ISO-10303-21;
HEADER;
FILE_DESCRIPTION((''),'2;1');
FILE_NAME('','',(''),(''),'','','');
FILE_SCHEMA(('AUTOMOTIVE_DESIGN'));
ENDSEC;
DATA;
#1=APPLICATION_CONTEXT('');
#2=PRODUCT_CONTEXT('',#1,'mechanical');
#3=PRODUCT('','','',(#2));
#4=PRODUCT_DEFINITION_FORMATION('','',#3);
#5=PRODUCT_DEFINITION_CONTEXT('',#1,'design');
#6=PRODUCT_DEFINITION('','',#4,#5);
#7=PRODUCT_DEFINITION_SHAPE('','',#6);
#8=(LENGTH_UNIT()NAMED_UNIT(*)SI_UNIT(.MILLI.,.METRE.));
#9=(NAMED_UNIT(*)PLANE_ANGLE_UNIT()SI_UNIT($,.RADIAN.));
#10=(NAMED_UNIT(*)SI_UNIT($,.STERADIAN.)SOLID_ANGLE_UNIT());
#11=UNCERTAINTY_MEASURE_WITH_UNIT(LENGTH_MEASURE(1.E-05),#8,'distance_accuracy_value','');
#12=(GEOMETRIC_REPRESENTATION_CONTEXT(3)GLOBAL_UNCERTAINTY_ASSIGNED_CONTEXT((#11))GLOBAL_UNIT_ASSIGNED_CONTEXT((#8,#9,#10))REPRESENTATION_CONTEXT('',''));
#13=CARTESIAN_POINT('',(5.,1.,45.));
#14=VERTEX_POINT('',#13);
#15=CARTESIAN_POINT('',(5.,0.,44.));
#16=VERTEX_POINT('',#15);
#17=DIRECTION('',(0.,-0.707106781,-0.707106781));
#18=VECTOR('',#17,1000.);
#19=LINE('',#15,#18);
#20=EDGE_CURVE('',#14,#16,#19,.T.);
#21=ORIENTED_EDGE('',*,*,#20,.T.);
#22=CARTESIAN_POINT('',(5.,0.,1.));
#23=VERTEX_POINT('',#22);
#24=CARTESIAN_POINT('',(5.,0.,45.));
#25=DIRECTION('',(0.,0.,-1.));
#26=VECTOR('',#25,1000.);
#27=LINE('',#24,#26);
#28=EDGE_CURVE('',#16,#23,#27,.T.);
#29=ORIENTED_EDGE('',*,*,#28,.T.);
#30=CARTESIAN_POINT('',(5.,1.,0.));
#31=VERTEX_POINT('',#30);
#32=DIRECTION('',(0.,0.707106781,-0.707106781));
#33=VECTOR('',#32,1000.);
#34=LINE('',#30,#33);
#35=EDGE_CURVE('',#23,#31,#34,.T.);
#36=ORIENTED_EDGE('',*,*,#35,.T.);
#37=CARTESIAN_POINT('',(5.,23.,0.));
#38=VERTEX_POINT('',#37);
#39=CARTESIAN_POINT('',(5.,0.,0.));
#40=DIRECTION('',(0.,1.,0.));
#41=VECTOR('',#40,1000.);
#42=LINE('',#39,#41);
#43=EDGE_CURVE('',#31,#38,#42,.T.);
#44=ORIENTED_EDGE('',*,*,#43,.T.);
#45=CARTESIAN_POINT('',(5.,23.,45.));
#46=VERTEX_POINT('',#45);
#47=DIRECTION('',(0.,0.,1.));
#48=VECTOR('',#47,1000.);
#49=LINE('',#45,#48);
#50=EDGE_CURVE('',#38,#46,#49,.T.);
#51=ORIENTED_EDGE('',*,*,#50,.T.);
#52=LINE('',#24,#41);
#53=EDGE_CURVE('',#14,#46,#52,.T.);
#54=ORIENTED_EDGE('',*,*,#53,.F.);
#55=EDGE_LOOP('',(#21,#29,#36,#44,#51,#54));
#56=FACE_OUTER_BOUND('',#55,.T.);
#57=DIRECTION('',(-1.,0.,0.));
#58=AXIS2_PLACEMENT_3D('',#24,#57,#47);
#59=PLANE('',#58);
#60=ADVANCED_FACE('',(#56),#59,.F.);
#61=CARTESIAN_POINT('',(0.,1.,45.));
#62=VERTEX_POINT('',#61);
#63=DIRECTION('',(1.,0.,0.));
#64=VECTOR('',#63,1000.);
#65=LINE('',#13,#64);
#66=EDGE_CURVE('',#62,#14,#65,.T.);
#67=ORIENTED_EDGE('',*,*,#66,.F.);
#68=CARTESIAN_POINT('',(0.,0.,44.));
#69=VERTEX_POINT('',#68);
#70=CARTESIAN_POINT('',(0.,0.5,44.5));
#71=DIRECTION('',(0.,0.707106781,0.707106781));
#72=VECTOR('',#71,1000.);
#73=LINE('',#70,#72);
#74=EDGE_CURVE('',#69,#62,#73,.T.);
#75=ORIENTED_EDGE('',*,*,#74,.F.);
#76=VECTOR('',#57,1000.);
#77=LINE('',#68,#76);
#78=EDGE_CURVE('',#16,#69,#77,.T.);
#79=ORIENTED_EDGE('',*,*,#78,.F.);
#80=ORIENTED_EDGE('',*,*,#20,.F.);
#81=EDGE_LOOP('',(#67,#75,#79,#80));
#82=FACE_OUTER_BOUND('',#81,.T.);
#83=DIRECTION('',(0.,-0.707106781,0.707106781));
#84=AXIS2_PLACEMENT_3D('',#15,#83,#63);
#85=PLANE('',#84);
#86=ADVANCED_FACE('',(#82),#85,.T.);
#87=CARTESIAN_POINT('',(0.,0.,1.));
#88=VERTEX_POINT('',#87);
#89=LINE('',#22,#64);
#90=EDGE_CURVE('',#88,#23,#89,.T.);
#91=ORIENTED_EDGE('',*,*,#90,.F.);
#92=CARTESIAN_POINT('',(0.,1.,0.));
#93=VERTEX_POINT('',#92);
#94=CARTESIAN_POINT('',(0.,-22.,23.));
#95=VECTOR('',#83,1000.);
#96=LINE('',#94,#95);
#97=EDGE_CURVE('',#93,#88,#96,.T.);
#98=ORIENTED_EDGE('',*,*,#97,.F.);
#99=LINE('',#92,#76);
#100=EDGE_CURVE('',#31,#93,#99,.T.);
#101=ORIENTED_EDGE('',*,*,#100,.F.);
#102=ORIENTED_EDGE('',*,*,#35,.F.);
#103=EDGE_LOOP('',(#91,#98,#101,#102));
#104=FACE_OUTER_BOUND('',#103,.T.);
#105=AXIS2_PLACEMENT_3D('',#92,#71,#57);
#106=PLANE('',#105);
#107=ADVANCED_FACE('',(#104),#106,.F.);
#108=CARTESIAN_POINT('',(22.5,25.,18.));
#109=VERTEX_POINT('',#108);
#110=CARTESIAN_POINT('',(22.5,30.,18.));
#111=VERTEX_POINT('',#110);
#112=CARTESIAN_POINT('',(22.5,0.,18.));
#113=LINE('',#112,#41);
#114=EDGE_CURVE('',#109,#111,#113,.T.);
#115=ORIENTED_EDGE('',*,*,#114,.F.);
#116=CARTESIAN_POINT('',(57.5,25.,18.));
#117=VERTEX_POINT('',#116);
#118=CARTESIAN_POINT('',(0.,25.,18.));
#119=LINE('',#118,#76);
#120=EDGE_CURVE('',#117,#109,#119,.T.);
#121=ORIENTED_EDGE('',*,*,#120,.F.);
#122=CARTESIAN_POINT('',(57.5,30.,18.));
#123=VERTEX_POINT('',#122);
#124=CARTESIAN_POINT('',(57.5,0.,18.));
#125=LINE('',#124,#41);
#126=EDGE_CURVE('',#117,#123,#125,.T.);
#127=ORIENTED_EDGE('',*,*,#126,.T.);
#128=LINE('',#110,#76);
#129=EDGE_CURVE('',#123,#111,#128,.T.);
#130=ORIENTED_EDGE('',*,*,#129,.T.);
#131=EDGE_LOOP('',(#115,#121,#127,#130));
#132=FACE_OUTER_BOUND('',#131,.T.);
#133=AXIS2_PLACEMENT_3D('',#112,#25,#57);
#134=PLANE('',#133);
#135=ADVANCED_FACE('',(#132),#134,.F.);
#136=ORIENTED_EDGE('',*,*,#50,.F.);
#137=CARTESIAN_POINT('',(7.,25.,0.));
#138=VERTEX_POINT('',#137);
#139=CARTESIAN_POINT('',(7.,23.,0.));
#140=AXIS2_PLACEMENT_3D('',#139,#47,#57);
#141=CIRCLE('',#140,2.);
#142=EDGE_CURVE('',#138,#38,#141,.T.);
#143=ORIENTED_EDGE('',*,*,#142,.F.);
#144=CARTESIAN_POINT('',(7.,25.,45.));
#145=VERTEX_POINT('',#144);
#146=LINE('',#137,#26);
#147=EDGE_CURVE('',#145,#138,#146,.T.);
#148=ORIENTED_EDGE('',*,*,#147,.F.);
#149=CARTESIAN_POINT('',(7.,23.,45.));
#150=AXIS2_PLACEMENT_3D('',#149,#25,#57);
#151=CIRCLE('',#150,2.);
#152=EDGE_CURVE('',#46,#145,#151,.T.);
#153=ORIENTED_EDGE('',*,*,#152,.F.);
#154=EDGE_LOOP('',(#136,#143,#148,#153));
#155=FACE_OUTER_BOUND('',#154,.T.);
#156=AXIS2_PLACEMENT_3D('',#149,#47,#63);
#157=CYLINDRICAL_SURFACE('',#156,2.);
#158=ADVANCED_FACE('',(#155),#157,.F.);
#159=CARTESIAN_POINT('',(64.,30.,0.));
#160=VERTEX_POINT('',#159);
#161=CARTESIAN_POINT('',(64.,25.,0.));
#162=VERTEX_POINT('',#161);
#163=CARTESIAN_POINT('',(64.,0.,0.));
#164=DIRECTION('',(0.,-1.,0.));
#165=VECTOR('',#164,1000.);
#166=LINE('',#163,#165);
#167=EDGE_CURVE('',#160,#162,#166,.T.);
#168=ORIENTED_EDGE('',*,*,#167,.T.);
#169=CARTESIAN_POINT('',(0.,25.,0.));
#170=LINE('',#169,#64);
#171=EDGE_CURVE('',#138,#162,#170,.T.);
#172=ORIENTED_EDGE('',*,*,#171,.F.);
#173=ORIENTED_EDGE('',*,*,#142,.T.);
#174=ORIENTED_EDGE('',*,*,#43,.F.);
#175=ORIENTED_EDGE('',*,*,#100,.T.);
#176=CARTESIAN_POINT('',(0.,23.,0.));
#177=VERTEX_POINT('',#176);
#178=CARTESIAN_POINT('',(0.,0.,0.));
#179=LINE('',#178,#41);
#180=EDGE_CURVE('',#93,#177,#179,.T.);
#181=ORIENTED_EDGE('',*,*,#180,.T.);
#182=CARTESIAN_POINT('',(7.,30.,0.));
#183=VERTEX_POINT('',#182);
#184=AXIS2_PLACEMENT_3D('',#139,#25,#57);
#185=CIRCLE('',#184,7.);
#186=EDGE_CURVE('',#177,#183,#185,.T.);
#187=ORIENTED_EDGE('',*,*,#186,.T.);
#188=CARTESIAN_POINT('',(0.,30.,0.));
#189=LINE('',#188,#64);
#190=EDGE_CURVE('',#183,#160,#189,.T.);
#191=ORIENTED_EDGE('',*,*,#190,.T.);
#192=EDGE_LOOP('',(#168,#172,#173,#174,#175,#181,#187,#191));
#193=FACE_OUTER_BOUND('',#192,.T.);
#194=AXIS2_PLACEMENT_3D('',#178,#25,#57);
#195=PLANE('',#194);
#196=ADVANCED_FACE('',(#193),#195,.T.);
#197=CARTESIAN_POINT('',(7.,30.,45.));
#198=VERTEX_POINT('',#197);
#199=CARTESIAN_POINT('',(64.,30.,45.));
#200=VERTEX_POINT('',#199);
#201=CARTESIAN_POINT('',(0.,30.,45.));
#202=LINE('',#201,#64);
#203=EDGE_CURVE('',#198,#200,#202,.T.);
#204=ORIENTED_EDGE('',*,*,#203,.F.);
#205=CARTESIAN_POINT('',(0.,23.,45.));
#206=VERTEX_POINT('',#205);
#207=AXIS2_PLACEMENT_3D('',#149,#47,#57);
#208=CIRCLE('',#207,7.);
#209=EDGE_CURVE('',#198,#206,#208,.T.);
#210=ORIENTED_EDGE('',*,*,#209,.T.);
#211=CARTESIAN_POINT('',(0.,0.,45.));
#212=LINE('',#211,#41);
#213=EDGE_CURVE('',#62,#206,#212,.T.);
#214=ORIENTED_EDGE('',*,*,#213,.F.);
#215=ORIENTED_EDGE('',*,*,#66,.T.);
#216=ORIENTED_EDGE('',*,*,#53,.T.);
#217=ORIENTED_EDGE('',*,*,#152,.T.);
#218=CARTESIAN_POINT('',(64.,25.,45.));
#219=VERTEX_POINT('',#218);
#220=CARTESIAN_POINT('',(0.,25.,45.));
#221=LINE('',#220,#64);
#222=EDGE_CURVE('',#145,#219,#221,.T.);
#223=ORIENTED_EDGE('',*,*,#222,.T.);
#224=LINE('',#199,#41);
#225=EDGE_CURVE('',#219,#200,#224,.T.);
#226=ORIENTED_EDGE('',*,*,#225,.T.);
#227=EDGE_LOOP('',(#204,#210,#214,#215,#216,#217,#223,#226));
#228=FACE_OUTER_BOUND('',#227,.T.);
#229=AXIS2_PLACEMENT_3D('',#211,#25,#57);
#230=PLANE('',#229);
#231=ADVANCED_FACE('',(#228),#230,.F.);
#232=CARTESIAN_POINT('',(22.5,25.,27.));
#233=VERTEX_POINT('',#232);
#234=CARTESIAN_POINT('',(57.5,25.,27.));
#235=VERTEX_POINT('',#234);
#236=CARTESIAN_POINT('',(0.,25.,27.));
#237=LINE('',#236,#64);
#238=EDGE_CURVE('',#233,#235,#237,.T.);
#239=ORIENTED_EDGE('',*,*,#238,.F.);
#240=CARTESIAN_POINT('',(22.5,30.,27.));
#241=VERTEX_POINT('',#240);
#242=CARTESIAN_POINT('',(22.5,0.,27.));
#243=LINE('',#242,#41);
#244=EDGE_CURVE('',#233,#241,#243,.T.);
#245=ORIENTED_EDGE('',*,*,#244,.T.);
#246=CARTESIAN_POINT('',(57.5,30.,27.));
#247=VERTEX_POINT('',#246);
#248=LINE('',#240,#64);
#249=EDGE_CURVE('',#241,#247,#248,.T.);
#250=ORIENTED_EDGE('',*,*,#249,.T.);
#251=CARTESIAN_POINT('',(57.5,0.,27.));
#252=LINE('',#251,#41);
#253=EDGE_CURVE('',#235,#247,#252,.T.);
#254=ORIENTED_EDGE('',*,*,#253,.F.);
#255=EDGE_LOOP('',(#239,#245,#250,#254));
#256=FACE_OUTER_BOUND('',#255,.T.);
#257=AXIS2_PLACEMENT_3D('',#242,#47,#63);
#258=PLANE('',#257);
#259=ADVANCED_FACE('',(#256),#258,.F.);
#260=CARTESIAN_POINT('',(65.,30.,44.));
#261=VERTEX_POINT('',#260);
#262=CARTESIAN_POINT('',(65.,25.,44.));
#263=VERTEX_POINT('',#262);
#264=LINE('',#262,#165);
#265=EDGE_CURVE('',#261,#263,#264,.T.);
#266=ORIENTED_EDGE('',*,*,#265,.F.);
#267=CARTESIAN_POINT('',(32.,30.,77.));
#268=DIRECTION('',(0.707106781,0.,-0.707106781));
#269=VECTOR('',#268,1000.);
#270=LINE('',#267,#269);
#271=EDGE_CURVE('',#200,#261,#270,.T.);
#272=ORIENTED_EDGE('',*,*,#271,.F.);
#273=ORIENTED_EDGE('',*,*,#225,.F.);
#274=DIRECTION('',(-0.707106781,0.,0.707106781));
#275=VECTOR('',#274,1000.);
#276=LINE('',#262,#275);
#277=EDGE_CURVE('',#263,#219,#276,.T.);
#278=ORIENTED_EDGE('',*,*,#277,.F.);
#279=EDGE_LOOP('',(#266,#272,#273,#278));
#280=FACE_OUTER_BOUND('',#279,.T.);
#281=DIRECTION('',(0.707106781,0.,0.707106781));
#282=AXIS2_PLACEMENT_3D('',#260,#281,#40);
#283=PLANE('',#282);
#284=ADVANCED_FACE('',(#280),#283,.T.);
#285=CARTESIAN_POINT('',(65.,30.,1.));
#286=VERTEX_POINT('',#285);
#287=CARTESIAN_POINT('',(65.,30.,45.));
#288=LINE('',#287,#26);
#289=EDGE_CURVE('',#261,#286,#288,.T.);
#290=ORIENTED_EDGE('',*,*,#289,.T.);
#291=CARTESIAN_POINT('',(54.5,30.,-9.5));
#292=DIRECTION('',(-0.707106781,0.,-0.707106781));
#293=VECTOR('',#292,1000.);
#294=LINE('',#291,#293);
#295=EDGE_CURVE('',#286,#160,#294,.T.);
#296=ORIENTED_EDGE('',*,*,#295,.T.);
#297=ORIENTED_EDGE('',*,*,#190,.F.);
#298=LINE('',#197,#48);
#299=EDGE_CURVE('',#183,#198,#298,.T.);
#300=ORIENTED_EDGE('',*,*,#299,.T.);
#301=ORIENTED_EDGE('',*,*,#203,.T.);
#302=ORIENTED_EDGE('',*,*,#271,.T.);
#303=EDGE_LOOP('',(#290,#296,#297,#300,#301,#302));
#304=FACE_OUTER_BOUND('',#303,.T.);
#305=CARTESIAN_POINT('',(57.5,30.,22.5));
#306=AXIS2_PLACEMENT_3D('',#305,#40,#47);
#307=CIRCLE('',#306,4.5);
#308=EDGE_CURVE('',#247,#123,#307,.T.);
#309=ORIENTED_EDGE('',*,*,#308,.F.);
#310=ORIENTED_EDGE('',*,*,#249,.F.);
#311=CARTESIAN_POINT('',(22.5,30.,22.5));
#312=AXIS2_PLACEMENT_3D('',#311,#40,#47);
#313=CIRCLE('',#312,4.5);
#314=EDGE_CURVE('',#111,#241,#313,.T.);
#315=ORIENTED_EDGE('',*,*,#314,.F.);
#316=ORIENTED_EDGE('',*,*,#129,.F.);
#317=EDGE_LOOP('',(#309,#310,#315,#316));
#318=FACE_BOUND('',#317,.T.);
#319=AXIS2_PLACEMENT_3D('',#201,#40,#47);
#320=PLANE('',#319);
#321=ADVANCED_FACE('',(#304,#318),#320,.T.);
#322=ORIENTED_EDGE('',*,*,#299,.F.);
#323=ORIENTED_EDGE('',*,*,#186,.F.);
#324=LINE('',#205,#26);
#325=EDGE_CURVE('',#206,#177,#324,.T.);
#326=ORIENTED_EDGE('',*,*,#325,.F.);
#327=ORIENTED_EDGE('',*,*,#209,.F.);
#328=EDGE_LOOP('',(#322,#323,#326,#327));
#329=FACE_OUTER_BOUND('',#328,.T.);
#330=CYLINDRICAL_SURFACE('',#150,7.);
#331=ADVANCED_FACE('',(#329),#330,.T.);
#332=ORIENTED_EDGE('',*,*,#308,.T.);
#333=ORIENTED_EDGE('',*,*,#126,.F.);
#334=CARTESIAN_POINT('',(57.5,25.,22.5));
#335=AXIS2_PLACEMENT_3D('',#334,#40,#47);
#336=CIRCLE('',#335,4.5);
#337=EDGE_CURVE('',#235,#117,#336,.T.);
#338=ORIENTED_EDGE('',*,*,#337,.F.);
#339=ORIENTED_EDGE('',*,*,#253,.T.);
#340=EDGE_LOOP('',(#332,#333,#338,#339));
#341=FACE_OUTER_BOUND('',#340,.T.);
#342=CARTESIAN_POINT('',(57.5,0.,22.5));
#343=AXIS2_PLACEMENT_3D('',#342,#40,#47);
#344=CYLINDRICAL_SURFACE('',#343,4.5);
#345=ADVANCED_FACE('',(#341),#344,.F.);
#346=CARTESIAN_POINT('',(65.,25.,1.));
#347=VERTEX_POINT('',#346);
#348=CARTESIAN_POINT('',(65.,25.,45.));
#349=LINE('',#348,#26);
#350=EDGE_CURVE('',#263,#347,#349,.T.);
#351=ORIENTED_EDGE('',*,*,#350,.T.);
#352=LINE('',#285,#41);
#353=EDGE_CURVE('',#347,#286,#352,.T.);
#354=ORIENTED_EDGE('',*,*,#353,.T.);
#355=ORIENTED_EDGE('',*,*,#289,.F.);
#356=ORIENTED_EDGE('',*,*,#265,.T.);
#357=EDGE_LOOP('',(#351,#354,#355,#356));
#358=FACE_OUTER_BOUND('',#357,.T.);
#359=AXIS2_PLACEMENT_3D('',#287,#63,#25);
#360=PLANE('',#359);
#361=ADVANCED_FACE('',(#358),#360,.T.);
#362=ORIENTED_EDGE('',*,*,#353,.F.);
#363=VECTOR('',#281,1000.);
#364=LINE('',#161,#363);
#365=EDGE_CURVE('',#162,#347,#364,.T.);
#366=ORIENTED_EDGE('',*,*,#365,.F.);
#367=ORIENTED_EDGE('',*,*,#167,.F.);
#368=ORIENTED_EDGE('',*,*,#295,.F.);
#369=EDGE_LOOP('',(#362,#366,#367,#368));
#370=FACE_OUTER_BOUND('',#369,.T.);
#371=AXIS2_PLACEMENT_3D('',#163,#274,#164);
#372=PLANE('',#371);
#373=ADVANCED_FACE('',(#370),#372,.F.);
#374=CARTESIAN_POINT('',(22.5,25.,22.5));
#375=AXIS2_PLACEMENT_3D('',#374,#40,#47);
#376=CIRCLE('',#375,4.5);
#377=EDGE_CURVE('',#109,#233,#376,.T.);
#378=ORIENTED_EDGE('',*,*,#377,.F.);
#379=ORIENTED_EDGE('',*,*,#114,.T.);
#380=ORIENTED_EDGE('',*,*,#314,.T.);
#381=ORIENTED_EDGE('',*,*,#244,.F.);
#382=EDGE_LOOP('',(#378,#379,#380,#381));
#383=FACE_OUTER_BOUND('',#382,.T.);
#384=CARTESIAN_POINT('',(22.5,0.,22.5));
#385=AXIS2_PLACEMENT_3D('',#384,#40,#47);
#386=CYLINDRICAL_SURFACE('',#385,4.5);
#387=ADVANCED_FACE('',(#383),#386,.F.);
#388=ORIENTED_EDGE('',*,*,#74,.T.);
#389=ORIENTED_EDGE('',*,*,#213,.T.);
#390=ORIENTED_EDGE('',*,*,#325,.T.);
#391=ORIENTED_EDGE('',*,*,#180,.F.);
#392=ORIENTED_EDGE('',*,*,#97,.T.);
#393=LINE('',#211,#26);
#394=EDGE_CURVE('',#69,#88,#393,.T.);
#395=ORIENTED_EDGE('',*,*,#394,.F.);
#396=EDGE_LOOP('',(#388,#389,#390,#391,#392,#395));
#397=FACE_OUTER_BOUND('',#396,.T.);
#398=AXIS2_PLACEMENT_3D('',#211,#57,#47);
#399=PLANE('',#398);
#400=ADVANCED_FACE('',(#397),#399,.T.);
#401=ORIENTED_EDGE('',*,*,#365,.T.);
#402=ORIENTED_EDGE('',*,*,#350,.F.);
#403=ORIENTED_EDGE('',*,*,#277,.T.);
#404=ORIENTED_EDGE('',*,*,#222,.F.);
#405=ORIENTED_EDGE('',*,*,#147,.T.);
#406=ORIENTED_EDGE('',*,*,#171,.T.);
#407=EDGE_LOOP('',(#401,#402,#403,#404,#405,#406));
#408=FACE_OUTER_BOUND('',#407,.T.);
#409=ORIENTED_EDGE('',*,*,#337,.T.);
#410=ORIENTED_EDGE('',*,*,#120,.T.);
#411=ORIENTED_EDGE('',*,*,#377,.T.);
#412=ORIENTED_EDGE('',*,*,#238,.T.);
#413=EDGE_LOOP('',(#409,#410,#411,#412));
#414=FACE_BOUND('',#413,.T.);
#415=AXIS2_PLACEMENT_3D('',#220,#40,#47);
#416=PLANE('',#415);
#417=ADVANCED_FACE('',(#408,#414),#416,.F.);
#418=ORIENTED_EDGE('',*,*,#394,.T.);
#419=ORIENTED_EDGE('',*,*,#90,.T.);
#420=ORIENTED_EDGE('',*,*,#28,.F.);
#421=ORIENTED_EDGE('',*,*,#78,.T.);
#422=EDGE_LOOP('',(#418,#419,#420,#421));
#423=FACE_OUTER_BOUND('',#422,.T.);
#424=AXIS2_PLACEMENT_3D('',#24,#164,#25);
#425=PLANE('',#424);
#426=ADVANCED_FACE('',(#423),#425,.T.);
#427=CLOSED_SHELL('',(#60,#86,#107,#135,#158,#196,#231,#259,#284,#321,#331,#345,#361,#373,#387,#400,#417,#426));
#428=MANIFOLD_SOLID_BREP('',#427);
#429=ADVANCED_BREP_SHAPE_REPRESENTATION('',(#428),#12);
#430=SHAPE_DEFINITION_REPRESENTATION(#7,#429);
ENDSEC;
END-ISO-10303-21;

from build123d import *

# Parameters (mm, degrees)
EXTRUDE_1_DEPTH     = 45
FILLET_1_R          = 2
FILLET_2_R          = 7
CHAMFER_1_SIZE      = 1
CUT_EXTRUDE_1_DEPTH = 85.557672626


with BuildPart() as part:
    # 草图1 → 拉伸-薄壁1 (new body)
    with BuildSketch(Plane.XY):
        Polygon((0, 0), (0, 30), (65, 30), (65, 25), (5, 25), (5, 0), align=None)
    extrude(amount=EXTRUDE_1_DEPTH)

    # 圆角1
    fillet_1_edges = [part.edges().sort_by_distance(p)[0] for p in [
        (5, 25, 22.5),
    ]]
    fillet(fillet_1_edges, radius=FILLET_1_R)

    # 圆角2
    fillet_2_edges = [part.edges().sort_by_distance(p)[0] for p in [
        (0, 30, 22.5),
    ]]
    fillet(fillet_2_edges, radius=FILLET_2_R)

    # 倒角1
    chamfer_1_edges = [part.edges().sort_by_distance(p)[0] for p in [
        (2.5, 0, 45),
        (2.5, 0, 0),
        (65, 27.5, 0),
        (65, 27.5, 45),
    ]]
    chamfer(chamfer_1_edges, length=CHAMFER_1_SIZE)

    # 草图2 → 切除-拉伸1 (cut, through all)
    with BuildSketch(Plane(origin=(0, 30, 0), x_dir=(1, 0, 0), z_dir=(0, 1, 0))):
        with BuildLine():
            Line((22.5, -18), (57.5, -18))
            ThreePointArc((57.5, -18), (62, -22.5), (57.5, -27))
            Line((57.5, -27), (22.5, -27))
            ThreePointArc((22.5, -27), (18, -22.5), (22.5, -18))
        make_face()
    extrude(amount=-CUT_EXTRUDE_1_DEPTH, mode=Mode.SUBTRACT)


solid = part.part
